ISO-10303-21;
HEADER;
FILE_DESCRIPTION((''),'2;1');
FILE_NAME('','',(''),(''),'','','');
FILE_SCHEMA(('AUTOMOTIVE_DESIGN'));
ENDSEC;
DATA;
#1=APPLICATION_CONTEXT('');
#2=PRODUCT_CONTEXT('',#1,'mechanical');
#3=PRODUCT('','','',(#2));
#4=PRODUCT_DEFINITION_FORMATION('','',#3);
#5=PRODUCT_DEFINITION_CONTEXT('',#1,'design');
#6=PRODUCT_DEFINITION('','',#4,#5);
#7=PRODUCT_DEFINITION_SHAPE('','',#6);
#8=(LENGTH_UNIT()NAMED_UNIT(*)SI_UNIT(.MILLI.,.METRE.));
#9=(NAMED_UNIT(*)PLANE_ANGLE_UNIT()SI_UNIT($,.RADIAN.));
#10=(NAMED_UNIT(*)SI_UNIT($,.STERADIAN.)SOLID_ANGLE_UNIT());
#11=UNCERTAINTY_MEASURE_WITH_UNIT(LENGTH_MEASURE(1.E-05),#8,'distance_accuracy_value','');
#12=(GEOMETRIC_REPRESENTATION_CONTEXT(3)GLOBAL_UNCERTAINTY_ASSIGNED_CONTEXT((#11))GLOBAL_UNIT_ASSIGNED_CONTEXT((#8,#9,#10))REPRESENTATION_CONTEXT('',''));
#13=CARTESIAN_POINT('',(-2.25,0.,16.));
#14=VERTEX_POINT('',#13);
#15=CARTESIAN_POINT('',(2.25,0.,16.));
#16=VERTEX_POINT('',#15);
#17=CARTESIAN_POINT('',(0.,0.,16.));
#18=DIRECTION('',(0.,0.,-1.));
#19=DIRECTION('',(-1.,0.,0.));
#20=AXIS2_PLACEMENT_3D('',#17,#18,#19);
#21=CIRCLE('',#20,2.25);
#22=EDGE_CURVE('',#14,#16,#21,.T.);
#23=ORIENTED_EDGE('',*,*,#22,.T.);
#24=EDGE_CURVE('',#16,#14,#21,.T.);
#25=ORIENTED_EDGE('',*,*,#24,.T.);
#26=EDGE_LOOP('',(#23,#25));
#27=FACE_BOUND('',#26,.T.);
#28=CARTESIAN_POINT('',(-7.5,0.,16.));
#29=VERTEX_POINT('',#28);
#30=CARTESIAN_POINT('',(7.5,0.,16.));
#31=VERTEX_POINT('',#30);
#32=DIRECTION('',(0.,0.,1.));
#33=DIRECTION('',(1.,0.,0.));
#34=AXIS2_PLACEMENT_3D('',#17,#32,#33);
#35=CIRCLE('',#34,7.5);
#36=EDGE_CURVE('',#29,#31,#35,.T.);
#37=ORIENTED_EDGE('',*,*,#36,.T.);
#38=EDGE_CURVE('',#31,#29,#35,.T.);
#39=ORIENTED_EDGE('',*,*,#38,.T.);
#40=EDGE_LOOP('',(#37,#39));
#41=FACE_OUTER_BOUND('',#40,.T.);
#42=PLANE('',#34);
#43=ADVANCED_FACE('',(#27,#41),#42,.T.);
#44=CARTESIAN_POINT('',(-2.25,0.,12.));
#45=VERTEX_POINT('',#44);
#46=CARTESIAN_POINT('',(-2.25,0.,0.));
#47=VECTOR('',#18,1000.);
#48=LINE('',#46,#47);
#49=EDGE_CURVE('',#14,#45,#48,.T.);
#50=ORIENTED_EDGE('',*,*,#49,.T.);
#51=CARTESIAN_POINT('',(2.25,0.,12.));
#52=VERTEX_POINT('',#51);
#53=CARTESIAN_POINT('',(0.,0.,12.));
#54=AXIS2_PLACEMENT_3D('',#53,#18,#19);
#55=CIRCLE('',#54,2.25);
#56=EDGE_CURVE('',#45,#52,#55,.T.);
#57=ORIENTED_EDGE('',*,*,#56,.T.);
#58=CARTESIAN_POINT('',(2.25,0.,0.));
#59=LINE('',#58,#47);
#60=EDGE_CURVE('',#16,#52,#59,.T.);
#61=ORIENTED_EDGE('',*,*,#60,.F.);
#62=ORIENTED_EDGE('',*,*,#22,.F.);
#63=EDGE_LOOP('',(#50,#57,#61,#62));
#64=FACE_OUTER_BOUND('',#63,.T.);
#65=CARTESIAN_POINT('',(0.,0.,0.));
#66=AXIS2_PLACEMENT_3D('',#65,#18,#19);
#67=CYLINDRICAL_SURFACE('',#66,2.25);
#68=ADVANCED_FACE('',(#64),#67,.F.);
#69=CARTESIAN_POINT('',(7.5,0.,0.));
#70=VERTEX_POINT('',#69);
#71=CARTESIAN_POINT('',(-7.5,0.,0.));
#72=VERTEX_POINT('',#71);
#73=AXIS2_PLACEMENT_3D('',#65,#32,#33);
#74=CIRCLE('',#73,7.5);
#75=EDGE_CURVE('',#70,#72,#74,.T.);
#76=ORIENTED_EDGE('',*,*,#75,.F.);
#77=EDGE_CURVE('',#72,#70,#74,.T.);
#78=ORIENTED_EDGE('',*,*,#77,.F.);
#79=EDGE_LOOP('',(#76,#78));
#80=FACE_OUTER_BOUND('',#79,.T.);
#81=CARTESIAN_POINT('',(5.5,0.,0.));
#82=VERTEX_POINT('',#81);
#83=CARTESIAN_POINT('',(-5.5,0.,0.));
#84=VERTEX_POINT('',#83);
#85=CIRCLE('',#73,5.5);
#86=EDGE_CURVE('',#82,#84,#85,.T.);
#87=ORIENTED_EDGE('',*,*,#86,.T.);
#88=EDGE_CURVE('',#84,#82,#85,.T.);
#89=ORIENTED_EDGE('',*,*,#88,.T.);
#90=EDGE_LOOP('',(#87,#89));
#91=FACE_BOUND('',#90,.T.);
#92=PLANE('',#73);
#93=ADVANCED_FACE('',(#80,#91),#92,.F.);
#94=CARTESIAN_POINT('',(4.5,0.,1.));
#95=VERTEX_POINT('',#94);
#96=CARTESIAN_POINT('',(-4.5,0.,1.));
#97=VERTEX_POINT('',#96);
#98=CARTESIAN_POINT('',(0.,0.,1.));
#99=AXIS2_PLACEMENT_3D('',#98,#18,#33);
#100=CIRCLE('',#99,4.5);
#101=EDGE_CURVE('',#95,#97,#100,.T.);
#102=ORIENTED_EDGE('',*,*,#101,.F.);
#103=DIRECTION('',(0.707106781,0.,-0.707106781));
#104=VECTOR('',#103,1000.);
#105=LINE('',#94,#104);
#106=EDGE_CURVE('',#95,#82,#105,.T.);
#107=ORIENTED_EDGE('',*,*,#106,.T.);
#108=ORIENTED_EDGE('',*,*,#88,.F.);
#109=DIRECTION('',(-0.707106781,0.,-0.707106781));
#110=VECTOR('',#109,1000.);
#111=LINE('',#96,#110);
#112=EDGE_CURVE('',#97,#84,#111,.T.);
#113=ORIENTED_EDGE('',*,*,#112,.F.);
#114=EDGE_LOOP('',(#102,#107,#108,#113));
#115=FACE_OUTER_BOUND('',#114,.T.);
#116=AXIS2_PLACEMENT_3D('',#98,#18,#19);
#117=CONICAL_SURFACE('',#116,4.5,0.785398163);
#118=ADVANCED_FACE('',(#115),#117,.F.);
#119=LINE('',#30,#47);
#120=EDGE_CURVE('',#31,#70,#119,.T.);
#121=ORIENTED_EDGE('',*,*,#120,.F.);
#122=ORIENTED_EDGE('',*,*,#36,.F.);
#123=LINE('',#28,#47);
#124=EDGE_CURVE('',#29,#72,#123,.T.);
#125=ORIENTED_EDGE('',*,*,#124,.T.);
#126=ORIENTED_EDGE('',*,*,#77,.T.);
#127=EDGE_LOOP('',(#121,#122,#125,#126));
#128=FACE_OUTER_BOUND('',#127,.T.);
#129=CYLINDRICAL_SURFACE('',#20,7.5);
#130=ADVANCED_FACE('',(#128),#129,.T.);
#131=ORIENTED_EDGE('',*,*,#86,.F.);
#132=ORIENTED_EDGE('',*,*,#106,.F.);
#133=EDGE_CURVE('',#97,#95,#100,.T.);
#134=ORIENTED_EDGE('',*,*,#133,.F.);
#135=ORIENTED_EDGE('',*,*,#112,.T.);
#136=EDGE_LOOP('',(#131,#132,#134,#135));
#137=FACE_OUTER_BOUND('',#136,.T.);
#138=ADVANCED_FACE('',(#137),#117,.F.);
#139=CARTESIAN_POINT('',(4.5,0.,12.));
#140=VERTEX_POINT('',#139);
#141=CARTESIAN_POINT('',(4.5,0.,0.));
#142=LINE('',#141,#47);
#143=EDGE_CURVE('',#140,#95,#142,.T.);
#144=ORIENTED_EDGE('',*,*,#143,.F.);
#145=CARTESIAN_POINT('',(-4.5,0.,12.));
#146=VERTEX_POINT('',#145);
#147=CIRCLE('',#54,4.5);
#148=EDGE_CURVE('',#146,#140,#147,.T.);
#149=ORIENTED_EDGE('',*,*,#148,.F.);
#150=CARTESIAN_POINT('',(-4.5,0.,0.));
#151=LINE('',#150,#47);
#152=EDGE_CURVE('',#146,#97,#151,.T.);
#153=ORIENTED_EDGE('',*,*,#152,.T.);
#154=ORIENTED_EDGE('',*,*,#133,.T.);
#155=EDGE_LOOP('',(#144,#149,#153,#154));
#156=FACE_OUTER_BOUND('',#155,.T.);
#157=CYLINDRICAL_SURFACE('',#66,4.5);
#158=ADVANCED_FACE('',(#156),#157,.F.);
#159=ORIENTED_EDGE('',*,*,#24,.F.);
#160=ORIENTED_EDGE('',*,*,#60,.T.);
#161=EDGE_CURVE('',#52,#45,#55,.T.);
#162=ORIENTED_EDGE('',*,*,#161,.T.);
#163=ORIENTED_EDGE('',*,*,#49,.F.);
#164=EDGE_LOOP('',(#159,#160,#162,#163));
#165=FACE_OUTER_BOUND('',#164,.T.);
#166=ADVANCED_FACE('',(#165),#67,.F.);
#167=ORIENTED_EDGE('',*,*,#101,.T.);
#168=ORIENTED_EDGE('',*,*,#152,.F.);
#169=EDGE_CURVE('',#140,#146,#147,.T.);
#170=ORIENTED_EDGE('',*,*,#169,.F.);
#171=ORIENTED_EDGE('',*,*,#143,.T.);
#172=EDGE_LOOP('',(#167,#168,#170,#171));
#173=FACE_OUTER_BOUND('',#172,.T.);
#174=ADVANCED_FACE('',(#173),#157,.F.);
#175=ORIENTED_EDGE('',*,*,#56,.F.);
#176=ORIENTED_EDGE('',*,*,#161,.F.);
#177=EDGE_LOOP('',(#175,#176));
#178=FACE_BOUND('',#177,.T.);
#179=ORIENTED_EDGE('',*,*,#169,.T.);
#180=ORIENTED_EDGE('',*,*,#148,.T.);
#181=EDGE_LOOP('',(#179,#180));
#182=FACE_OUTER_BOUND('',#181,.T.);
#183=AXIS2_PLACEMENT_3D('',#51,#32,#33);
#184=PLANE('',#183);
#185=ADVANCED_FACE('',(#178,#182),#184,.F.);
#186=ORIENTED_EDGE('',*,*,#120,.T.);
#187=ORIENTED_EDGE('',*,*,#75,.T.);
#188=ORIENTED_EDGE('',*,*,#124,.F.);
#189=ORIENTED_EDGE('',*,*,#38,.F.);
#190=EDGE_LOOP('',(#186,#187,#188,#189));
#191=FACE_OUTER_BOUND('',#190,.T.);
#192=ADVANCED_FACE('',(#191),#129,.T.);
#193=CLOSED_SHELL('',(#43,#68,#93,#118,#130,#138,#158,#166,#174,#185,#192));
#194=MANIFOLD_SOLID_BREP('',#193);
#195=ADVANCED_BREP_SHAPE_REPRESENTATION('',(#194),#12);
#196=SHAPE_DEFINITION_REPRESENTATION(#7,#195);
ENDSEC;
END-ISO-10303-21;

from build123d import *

# Parameters (mm, degrees)
SKETCH_1_R                   = 7.5
EXTRUDE_1_DEPTH              = 16
HOLE_WIZARD_M4_1_D           = 4.5
HOLE_WIZARD_M4_1_CBORE_D     = 9
HOLE_WIZARD_M4_1_CBORE_DEPTH = 12
CHAMFER_1_SIZE               = 1


with BuildPart() as part:
    # 草图1 → 凸台-拉伸1 (new body)
    with BuildSketch(Plane.XY):
        Circle(SKETCH_1_R)
    extrude(amount=EXTRUDE_1_DEPTH)

    # M4 六角凹头螺钉的柱形沉头孔1 (through all)
    with Locations(Plane(origin=(0, 0, 0), x_dir=(-1, 0, 0), z_dir=(0, 0, -1))):
        with Locations((0, 0)):
            CounterBoreHole(HOLE_WIZARD_M4_1_D / 2, HOLE_WIZARD_M4_1_CBORE_D / 2, HOLE_WIZARD_M4_1_CBORE_DEPTH)

    # 倒角1
    chamfer_1_edges = [part.edges().sort_by_distance(p)[0] for p in [
        (4.5, 0, 0),
    ]]
    chamfer(chamfer_1_edges, length=CHAMFER_1_SIZE)


solid = part.part
